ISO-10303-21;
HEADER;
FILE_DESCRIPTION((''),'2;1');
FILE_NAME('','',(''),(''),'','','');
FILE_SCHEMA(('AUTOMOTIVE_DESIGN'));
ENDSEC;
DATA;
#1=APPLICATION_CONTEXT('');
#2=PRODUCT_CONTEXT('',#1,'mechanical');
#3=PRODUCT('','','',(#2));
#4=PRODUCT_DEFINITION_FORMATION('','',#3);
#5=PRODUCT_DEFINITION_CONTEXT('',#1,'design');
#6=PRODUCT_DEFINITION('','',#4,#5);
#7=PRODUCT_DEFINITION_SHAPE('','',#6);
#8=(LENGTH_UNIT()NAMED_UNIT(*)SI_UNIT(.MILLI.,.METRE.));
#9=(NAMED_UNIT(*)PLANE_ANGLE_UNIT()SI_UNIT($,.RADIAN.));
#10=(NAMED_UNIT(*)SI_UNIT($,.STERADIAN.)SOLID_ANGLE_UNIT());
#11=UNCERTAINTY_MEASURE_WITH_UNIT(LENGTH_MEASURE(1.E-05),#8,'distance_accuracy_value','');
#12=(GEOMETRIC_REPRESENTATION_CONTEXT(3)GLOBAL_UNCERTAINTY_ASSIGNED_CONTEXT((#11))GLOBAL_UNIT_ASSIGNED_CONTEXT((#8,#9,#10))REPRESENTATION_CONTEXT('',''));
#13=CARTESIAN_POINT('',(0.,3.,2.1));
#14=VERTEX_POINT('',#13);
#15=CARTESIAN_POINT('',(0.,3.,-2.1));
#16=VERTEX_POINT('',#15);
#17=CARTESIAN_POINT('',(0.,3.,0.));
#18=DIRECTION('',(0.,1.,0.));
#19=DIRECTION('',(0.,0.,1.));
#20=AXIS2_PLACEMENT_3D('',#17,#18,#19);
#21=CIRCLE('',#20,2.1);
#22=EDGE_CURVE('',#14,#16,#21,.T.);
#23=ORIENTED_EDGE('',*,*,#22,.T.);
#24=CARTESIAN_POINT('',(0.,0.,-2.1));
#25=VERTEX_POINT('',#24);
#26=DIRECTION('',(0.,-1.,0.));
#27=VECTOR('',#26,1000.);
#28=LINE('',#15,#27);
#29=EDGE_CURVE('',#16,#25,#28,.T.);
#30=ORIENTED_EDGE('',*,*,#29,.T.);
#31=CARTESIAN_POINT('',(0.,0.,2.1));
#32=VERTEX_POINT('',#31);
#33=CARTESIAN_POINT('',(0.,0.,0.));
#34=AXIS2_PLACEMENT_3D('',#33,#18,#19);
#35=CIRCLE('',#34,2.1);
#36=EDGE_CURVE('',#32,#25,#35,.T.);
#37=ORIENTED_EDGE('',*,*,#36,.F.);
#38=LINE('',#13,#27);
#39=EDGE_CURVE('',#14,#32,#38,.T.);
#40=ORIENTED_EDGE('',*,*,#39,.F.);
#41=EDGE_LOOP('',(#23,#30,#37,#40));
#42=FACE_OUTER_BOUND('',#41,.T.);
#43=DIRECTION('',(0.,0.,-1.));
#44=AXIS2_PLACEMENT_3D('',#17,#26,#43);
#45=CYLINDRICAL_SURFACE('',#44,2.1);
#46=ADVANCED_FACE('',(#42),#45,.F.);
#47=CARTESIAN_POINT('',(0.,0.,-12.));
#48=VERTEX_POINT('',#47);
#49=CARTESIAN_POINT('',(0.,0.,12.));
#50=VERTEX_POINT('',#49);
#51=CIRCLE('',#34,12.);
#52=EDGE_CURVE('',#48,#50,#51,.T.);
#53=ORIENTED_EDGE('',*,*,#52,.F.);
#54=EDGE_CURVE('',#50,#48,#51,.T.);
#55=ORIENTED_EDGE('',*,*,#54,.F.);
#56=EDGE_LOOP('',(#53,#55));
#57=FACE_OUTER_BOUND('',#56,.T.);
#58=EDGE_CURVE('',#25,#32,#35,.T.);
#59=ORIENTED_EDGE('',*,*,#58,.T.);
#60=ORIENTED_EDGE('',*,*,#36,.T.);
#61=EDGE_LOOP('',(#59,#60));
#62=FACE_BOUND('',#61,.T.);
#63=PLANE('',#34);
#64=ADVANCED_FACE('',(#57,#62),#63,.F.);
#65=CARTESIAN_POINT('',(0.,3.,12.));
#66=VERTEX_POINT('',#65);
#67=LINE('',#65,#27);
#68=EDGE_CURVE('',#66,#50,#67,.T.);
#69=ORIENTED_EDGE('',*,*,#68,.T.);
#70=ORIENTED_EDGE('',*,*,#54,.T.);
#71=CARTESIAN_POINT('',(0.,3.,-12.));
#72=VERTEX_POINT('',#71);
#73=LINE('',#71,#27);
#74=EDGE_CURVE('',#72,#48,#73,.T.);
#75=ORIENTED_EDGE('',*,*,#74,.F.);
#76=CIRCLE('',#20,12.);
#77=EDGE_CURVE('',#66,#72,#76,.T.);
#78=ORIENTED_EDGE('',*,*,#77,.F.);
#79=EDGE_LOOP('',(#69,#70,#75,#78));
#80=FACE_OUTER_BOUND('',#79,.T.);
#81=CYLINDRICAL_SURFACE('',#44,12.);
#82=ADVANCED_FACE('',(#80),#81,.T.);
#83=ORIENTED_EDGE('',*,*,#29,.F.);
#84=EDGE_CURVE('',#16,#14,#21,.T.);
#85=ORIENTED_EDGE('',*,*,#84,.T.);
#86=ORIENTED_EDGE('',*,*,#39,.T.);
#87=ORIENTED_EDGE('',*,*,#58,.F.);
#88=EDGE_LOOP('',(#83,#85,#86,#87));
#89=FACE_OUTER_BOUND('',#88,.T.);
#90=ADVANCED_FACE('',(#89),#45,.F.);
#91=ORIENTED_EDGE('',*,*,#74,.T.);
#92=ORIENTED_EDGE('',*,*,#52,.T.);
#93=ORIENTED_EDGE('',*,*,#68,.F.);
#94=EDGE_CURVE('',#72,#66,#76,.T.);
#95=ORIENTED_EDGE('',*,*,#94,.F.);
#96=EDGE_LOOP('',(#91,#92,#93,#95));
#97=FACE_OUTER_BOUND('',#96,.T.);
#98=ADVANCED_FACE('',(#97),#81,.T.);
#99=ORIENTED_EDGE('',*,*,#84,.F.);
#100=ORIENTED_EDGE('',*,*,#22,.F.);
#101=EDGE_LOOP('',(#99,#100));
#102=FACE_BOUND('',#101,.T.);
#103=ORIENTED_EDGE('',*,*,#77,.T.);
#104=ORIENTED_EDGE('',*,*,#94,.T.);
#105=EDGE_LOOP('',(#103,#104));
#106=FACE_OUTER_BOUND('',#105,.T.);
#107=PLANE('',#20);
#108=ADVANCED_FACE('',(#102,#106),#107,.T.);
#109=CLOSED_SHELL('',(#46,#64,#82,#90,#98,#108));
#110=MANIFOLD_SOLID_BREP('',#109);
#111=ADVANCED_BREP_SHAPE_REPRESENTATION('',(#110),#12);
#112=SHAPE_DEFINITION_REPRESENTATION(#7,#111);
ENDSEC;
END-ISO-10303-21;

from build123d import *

# Parameters (mm, degrees)
SKETCH_1_R      = 12
SKETCH_1_R_2    = 2.1
EXTRUDE_1_DEPTH = 3


with BuildPart() as part:
    # 草图1 → 凸台-拉伸1 (new body)
    with BuildSketch(Plane(origin=(0, 0, 0), x_dir=(1, 0, 0), z_dir=(0, 1, 0))):
        with Locations(Location((0, 0, 0), (0, 0, 270))):
            Circle(SKETCH_1_R)
        with Locations(Location((0, 0, 0), (0, 0, 270))):
            Circle(SKETCH_1_R_2, mode=Mode.SUBTRACT)
    extrude(amount=EXTRUDE_1_DEPTH)


solid = part.part
